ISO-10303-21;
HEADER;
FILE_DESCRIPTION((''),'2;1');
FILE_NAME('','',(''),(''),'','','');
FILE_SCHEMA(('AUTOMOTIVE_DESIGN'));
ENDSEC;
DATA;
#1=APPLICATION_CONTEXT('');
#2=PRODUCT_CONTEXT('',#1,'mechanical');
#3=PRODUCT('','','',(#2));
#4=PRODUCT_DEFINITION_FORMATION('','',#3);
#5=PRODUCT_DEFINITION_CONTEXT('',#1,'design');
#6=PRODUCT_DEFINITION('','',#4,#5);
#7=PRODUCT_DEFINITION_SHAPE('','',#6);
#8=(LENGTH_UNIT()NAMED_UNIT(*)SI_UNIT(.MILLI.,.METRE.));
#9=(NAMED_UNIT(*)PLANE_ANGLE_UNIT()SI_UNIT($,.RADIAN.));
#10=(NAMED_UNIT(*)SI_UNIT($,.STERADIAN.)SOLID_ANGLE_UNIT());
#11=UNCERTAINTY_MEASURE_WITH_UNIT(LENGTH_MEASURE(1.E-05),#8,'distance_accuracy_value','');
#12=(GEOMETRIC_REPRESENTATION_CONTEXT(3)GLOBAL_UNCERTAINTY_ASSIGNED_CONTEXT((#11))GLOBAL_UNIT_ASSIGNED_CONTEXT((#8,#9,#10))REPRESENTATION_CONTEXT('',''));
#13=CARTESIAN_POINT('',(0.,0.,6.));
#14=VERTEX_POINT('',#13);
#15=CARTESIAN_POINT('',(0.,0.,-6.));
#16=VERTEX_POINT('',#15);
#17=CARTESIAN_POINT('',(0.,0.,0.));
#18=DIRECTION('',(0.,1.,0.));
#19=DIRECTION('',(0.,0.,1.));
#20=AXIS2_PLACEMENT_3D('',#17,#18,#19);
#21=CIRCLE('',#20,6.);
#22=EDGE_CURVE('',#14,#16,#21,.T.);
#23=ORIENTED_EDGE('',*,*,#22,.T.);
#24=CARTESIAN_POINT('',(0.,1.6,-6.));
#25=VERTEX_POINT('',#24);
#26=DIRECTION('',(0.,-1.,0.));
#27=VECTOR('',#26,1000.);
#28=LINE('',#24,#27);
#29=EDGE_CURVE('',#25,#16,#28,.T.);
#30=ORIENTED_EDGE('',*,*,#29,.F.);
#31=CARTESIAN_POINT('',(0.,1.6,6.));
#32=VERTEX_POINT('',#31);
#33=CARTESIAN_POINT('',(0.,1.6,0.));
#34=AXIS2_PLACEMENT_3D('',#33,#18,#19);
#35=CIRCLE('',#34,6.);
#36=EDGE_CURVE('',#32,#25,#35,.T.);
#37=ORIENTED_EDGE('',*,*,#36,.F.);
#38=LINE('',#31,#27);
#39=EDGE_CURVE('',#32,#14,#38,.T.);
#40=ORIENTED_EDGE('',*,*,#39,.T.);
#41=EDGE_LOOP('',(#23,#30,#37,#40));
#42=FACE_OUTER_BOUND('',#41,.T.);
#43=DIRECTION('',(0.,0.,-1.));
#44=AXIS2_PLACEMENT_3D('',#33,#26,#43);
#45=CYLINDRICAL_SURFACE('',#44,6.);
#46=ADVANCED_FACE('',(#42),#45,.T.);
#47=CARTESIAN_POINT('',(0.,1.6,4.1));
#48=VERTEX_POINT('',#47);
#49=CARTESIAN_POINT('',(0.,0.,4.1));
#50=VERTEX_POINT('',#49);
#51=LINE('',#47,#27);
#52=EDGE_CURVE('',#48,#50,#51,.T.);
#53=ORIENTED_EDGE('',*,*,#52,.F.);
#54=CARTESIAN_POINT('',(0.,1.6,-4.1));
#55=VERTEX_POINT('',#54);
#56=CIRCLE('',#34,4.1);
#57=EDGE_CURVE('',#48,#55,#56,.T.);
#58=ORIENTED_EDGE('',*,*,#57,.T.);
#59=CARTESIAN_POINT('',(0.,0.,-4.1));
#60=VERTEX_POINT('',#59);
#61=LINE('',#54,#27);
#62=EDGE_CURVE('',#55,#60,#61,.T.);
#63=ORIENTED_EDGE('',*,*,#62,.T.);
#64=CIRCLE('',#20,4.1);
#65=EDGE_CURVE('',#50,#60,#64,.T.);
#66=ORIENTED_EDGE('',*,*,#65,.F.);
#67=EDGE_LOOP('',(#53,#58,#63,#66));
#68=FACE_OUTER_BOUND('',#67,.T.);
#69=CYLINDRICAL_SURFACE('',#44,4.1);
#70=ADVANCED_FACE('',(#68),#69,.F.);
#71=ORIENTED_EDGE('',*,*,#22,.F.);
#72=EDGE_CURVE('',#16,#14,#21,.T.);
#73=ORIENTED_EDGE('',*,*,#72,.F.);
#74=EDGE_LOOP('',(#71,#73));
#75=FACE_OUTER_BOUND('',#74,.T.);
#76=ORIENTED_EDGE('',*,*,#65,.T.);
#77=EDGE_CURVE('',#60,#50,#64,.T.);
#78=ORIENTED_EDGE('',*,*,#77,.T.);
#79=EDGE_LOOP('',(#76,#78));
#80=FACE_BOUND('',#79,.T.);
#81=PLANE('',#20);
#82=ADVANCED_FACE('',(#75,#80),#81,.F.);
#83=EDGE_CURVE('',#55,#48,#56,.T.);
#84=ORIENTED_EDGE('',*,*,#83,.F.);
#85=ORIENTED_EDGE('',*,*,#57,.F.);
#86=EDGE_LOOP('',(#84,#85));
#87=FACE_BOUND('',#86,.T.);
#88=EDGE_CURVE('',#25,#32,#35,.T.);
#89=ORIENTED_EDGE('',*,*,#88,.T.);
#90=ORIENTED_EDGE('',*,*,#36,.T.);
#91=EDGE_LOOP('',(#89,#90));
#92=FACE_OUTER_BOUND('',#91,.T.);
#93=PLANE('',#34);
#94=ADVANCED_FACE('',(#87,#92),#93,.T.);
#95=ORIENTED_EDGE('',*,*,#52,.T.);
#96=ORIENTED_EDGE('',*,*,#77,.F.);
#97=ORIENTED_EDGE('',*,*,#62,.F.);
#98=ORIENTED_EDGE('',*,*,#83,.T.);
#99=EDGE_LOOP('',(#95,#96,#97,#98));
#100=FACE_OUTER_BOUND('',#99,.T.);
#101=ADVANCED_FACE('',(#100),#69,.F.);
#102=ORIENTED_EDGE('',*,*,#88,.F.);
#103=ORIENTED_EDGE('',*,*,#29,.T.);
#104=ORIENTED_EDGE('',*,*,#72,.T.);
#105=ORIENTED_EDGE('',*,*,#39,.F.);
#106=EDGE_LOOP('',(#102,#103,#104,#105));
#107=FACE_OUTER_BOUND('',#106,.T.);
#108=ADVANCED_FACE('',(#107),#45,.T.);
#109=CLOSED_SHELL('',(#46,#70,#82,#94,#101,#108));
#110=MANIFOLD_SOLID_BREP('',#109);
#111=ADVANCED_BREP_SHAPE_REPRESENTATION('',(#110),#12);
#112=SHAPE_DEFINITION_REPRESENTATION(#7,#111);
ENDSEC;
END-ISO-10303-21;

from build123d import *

# Parameters (mm, degrees)
SKETCH1_R           = 6
SKETCH1_R_2         = 4.1
BOSS_EXTRUDE1_DEPTH = 1.6


with BuildPart() as part:
    # Sketch1 → Boss-Extrude1 (new body)
    with BuildSketch(Plane(origin=(0, 0, 0), x_dir=(1, 0, 0), z_dir=(0, 1, 0))):
        with Locations(Location((0, 0, 0), (0, 0, 270))):
            Circle(SKETCH1_R)
        with Locations(Location((0, 0, 0), (0, 0, 270))):
            Circle(SKETCH1_R_2, mode=Mode.SUBTRACT)
    extrude(amount=BOSS_EXTRUDE1_DEPTH)


solid = part.part
